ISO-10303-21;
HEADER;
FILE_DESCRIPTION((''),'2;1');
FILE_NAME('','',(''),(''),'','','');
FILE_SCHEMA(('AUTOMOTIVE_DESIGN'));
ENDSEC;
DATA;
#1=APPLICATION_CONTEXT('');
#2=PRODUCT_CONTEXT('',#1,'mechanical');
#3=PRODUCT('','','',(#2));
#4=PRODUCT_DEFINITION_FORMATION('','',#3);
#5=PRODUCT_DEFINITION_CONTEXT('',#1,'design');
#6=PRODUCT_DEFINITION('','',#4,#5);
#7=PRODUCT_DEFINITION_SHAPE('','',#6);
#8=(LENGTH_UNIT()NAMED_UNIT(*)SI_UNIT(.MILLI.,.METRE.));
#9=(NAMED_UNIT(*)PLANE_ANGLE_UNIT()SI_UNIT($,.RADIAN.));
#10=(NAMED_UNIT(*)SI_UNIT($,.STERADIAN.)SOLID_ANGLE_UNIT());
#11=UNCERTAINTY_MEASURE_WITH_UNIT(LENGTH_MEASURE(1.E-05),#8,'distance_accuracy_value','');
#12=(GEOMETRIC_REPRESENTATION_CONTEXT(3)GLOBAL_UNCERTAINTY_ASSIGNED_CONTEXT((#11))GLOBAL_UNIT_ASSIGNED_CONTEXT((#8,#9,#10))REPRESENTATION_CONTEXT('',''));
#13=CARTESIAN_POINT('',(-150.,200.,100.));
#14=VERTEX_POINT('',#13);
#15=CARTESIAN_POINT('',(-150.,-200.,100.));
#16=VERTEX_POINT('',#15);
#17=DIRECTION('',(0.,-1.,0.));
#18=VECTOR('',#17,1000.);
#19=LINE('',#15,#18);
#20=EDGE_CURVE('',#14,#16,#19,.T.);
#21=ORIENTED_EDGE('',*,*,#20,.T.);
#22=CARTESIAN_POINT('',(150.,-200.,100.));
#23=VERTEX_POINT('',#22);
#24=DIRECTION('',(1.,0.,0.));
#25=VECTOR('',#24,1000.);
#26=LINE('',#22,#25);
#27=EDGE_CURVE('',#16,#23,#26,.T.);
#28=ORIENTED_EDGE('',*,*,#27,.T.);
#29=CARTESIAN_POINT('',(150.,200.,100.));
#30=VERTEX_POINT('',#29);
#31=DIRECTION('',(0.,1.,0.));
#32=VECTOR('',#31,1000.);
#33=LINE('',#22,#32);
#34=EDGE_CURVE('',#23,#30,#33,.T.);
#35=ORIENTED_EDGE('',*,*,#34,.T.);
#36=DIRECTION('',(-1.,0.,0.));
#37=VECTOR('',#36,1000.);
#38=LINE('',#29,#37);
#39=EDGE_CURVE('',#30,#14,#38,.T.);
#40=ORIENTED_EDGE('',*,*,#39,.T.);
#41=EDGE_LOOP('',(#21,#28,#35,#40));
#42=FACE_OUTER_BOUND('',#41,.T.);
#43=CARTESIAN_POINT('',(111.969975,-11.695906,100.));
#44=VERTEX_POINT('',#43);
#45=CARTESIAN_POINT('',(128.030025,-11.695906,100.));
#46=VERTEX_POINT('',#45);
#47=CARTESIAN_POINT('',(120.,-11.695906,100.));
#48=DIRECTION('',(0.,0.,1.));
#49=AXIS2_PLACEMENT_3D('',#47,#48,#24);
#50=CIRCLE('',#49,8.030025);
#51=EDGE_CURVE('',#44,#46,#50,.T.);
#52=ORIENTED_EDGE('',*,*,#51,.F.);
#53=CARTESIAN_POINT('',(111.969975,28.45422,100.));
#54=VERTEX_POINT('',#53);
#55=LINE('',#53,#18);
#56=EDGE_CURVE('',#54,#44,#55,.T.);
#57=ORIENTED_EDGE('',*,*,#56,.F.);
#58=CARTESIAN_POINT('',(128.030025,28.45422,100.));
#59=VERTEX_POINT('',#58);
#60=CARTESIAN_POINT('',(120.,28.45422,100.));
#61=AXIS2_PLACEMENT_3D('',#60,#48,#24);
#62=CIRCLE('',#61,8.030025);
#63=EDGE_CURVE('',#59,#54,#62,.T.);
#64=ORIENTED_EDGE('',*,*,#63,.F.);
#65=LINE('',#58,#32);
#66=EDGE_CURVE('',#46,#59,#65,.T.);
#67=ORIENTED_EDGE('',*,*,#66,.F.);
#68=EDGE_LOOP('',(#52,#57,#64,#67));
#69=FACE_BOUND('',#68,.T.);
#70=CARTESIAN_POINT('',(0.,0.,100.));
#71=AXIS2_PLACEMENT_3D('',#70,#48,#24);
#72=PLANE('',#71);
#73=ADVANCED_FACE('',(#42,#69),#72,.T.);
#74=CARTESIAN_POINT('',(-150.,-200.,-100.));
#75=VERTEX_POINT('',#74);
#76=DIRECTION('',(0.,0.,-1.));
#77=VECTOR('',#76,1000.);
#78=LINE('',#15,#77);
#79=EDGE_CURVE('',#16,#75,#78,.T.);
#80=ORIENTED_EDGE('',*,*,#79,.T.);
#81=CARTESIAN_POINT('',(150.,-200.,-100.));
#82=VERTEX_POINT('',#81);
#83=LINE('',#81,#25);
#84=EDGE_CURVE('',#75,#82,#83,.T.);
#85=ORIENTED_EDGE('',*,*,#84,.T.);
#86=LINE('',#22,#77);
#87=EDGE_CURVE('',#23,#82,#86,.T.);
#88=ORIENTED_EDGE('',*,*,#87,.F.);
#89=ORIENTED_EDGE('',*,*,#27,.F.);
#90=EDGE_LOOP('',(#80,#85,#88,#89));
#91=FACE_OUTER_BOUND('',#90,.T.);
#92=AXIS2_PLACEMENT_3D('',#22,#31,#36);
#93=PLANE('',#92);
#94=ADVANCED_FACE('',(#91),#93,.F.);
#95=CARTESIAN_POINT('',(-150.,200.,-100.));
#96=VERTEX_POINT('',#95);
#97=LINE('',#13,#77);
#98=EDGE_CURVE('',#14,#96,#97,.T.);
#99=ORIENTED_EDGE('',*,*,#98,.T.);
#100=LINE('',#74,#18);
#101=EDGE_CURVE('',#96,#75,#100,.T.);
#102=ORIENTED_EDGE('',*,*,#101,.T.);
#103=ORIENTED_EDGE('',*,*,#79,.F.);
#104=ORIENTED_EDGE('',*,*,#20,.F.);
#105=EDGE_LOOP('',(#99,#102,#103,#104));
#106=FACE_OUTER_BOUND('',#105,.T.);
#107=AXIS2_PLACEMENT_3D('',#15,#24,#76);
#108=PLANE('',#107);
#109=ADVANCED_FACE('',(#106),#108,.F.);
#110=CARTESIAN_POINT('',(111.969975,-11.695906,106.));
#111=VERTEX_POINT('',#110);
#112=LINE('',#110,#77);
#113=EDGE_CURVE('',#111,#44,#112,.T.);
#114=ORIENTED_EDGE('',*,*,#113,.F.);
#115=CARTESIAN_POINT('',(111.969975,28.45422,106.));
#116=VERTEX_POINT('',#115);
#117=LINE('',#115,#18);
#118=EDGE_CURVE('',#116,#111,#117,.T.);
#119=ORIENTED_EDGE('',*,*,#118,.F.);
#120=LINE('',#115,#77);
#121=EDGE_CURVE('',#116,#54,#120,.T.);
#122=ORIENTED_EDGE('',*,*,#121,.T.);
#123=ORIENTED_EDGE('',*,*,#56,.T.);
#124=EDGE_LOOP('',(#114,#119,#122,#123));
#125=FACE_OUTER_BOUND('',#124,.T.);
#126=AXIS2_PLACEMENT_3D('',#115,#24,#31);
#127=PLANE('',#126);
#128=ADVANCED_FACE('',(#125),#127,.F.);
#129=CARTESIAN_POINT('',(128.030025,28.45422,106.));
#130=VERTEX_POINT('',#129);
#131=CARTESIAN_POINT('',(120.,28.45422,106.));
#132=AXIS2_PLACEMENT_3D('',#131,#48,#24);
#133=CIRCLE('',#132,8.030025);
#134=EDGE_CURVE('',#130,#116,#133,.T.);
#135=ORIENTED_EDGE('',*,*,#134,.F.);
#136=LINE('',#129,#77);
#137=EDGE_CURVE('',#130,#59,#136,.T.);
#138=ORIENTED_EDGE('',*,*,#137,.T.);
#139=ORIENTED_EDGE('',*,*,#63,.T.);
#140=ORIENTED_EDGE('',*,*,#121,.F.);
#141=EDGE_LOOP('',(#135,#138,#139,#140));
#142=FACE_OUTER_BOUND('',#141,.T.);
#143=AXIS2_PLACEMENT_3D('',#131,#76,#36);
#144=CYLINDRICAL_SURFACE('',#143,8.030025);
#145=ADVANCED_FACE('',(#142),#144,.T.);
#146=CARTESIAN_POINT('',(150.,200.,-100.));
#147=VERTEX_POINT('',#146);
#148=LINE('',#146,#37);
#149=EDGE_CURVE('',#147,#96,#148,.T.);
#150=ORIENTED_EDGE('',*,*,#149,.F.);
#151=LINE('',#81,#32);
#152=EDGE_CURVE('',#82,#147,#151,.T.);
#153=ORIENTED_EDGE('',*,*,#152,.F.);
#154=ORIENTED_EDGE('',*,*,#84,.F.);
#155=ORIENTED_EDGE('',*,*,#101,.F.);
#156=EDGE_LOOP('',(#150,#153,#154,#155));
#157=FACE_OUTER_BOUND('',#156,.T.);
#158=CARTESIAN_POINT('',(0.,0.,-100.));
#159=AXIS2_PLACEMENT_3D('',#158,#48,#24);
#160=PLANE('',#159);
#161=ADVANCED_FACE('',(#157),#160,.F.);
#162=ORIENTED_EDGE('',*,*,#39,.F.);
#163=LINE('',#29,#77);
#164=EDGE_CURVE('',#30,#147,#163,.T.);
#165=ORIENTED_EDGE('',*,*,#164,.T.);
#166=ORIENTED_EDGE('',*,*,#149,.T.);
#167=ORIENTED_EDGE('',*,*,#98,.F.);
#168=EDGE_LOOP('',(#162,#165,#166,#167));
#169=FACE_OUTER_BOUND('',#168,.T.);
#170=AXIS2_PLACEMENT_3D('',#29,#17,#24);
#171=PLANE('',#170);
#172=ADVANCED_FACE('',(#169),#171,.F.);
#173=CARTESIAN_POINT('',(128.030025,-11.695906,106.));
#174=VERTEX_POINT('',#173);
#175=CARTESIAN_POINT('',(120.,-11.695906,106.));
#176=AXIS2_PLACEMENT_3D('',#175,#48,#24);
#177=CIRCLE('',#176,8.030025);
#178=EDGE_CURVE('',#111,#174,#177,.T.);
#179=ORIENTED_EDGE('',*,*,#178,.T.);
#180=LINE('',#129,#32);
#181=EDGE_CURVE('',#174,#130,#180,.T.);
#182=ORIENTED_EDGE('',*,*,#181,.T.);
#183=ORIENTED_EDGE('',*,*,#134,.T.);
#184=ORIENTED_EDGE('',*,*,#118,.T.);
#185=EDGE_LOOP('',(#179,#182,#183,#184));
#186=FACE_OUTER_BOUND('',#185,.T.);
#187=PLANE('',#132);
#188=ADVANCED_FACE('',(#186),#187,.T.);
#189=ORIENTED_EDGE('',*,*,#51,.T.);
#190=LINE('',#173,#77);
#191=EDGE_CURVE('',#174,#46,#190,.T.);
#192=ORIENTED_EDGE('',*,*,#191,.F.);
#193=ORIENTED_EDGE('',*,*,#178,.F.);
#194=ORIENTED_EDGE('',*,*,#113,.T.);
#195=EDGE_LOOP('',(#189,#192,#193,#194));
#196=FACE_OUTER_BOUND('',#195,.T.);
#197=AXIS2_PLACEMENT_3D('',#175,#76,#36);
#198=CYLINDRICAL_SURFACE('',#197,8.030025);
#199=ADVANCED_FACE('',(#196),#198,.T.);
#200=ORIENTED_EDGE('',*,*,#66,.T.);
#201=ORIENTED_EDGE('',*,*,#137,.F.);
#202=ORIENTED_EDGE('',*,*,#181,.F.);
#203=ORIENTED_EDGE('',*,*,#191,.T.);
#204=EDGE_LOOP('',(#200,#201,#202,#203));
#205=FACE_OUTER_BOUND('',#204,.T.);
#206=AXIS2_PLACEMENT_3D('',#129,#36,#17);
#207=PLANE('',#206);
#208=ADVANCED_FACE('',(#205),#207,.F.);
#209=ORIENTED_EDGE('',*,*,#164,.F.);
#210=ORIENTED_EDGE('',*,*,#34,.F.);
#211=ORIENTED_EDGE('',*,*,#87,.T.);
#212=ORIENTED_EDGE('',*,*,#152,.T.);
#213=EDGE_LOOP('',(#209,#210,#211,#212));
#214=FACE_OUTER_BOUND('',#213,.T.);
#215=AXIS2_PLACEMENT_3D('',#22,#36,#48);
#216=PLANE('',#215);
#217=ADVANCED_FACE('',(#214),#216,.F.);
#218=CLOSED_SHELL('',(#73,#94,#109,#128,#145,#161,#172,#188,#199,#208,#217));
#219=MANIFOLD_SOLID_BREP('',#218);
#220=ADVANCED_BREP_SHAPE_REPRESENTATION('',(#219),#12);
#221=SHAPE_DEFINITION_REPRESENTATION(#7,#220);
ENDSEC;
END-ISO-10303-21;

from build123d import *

# Parameters (mm, degrees)
SKETCH_1_W      = 300
SKETCH_1_H      = 400
EXTRUDE_1_DEPTH = 100
EXTRUDE_2_DEPTH = 6


with BuildPart() as part:
    # 草图1 → 凸台-拉伸1 (new, symmetric)
    with BuildSketch(Plane.XY):
        Rectangle(SKETCH_1_W, SKETCH_1_H)
    extrude(amount=EXTRUDE_1_DEPTH, both=True)

    # 草图2 → 凸台-拉伸2 (add)
    with BuildSketch(Plane.XY.offset(100)):
        with BuildLine():
            Line((128.030025312, 28.454220127), (128.030025312, -11.695906433))
            ThreePointArc((128.030025312, -11.695906433), (120, -19.725931745), (111.969974688, -11.695906433))
            Line((111.969974688, -11.695906433), (111.969974688, 28.454220127))
            ThreePointArc((111.969974688, 28.454220127), (120, 36.484245439), (128.030025312, 28.454220127))
        make_face()
    extrude(amount=EXTRUDE_2_DEPTH)


solid = part.part
